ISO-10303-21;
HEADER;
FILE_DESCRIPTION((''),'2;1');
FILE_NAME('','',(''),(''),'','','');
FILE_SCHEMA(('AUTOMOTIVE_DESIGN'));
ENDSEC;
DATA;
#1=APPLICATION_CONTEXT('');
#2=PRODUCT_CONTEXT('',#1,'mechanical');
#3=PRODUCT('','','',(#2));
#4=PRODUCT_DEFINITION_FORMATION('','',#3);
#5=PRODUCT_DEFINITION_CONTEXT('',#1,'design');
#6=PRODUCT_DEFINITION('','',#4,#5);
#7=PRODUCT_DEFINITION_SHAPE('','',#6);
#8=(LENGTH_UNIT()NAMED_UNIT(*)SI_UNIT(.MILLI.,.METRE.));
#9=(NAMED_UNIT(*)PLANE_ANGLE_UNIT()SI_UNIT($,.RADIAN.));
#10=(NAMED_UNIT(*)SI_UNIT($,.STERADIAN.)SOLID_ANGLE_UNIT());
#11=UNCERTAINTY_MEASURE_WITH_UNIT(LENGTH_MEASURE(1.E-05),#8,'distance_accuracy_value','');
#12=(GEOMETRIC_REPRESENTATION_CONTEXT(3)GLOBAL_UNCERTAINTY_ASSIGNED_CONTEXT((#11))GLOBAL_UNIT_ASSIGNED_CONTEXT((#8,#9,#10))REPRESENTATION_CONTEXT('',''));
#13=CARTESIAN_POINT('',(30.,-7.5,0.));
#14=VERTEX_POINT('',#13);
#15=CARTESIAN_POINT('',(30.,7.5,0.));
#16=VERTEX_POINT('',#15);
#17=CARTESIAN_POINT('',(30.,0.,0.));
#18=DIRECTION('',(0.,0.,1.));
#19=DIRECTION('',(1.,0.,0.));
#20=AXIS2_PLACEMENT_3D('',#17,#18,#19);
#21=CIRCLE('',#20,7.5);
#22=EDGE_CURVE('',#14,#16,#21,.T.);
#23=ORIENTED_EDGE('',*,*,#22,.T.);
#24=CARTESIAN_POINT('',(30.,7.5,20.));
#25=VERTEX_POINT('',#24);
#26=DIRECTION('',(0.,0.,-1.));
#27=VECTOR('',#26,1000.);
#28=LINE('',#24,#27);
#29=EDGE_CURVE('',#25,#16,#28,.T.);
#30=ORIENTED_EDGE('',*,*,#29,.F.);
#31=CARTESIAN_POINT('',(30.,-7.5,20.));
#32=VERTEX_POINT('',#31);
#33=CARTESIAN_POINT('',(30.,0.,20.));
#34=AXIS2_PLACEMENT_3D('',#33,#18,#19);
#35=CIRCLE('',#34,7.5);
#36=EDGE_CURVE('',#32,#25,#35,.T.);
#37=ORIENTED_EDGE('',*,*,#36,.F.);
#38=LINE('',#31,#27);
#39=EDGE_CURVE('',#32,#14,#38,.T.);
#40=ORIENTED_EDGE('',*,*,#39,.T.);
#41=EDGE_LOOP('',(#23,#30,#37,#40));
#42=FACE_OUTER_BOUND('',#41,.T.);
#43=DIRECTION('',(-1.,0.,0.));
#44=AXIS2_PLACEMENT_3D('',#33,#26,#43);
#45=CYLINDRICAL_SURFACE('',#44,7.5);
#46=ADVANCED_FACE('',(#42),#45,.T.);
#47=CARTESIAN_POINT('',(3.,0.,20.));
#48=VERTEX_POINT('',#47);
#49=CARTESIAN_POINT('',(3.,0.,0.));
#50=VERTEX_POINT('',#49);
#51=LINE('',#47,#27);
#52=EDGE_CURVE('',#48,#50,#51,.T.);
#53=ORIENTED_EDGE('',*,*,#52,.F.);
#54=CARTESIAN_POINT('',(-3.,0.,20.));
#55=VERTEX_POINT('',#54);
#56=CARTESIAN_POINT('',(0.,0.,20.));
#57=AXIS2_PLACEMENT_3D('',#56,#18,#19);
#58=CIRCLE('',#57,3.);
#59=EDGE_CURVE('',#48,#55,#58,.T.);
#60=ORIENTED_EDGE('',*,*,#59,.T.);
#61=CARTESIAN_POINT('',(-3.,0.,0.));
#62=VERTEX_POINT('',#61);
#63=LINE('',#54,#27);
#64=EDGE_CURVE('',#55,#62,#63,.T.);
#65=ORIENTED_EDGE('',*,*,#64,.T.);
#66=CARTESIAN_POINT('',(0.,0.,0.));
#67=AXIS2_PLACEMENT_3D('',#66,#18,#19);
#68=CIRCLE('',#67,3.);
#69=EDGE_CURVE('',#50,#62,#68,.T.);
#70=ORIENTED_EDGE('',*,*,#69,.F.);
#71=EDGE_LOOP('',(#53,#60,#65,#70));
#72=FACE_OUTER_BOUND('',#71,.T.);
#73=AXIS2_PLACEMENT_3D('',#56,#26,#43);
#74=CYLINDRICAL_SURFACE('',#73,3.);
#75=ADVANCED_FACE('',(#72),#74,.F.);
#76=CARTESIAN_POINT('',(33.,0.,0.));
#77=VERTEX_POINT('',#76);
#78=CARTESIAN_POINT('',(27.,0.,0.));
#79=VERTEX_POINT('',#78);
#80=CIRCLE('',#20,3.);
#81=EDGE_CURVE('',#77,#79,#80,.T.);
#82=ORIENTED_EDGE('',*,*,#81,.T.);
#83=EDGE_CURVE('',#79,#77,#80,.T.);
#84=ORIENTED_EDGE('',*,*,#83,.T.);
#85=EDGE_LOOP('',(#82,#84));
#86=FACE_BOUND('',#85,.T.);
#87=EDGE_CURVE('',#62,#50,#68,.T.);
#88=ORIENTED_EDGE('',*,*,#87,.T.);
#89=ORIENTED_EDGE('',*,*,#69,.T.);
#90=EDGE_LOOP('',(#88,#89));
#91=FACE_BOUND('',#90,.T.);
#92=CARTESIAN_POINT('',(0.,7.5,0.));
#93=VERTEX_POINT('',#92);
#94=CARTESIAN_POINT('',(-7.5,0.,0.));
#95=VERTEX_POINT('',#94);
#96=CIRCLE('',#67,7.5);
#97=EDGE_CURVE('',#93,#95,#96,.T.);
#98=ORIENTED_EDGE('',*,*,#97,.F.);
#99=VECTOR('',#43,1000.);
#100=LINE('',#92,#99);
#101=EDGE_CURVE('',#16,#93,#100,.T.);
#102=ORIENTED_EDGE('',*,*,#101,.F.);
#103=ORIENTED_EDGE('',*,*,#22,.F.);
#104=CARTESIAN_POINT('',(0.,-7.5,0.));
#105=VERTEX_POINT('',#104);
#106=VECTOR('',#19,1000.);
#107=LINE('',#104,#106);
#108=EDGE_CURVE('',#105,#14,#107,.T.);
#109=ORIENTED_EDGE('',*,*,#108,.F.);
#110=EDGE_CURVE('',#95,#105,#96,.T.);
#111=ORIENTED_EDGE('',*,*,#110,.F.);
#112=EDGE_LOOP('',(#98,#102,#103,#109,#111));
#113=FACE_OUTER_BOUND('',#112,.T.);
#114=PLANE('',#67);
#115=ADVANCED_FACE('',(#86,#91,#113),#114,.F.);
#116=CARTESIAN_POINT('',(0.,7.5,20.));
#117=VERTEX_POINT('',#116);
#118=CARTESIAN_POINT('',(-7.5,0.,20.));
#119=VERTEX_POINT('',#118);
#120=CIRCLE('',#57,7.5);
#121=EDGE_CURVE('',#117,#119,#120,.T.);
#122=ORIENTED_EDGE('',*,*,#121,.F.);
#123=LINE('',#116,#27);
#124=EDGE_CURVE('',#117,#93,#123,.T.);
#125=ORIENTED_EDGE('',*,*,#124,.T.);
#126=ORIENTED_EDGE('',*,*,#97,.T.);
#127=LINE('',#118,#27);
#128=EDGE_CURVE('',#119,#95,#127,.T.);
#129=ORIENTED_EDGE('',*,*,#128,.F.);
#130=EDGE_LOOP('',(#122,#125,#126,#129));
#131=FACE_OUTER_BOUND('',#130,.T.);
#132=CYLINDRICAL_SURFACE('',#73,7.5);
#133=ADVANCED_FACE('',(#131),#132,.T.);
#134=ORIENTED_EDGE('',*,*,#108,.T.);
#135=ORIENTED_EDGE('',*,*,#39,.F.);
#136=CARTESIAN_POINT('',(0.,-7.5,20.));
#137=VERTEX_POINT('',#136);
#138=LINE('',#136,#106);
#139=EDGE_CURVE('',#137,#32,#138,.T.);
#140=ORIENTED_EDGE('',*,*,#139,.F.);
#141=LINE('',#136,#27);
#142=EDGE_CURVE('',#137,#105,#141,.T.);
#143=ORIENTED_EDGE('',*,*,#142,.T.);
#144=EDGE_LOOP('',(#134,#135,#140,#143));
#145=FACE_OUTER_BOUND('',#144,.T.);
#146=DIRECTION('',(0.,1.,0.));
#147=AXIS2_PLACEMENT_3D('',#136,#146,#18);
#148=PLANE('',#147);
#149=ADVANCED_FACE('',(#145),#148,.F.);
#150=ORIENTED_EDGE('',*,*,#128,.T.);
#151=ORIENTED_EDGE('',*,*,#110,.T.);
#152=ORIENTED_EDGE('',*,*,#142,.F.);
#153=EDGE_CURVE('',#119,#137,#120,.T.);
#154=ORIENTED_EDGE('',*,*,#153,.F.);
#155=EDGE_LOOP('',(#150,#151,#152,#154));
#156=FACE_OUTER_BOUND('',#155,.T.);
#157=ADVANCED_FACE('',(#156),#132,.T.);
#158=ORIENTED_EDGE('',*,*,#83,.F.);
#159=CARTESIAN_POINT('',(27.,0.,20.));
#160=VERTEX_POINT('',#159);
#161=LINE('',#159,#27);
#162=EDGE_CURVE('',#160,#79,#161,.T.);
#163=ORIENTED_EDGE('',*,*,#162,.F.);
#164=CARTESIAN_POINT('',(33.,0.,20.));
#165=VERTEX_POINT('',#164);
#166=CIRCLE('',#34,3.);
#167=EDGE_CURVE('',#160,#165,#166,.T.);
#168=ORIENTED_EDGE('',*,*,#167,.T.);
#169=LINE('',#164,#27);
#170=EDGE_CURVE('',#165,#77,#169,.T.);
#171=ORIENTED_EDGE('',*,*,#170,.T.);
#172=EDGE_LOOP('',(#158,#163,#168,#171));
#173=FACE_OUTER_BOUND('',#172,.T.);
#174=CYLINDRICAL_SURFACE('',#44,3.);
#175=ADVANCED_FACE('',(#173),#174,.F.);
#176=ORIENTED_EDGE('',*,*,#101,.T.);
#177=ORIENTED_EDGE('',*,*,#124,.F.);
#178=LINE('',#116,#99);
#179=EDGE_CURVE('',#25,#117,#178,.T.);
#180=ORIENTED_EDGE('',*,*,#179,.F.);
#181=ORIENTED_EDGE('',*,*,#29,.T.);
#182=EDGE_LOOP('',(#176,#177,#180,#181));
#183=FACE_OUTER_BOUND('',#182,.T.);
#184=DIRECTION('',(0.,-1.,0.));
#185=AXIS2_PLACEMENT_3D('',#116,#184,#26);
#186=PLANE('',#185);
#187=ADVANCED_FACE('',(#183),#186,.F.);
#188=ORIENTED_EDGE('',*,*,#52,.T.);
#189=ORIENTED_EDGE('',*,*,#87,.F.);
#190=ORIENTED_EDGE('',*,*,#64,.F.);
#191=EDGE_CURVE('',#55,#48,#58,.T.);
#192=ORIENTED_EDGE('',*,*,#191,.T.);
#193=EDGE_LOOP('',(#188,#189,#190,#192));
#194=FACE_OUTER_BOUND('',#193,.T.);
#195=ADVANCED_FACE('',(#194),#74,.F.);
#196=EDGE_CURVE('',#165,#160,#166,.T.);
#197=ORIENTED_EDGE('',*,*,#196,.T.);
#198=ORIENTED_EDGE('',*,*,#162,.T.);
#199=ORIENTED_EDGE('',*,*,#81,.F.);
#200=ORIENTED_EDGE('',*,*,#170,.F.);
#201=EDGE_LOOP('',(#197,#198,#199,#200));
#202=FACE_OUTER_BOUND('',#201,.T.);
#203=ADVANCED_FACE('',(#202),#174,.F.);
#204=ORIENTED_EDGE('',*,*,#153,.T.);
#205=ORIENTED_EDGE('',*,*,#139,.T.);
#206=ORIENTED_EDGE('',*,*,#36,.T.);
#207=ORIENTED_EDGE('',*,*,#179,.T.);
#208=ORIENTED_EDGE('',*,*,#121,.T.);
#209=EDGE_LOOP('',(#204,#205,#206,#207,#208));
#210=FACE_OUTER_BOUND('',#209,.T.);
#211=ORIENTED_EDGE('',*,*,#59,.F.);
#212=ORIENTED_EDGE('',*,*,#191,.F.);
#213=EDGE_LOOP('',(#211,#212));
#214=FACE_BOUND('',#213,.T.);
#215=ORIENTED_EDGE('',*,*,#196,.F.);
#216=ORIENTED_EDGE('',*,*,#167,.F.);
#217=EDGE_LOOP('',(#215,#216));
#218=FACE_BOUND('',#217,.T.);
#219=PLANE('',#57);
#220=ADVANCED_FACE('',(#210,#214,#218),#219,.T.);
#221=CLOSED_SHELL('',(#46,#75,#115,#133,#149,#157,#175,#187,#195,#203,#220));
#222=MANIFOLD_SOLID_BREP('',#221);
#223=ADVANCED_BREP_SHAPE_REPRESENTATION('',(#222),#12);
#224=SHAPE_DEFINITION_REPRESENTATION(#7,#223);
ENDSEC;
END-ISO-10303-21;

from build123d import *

# Parameters (mm, degrees)
SKETCH1_R           = 3
BOSS_EXTRUDE1_DEPTH = 20


with BuildPart() as part:
    # Sketch1 → Boss-Extrude1 (new body)
    with BuildSketch(Plane.XY):
        with BuildLine():
            Line((0, 7.5), (30, 7.5))
            ThreePointArc((30, 7.5), (37.5, 0), (30, -7.5))
            Line((30, -7.5), (0, -7.5))
            ThreePointArc((0, -7.5), (-7.5, 0), (0, 7.5))
        make_face()
        Circle(SKETCH1_R, mode=Mode.SUBTRACT)
        with Locations((30, 0)):
            Circle(SKETCH1_R, mode=Mode.SUBTRACT)
    extrude(amount=BOSS_EXTRUDE1_DEPTH)


solid = part.part
